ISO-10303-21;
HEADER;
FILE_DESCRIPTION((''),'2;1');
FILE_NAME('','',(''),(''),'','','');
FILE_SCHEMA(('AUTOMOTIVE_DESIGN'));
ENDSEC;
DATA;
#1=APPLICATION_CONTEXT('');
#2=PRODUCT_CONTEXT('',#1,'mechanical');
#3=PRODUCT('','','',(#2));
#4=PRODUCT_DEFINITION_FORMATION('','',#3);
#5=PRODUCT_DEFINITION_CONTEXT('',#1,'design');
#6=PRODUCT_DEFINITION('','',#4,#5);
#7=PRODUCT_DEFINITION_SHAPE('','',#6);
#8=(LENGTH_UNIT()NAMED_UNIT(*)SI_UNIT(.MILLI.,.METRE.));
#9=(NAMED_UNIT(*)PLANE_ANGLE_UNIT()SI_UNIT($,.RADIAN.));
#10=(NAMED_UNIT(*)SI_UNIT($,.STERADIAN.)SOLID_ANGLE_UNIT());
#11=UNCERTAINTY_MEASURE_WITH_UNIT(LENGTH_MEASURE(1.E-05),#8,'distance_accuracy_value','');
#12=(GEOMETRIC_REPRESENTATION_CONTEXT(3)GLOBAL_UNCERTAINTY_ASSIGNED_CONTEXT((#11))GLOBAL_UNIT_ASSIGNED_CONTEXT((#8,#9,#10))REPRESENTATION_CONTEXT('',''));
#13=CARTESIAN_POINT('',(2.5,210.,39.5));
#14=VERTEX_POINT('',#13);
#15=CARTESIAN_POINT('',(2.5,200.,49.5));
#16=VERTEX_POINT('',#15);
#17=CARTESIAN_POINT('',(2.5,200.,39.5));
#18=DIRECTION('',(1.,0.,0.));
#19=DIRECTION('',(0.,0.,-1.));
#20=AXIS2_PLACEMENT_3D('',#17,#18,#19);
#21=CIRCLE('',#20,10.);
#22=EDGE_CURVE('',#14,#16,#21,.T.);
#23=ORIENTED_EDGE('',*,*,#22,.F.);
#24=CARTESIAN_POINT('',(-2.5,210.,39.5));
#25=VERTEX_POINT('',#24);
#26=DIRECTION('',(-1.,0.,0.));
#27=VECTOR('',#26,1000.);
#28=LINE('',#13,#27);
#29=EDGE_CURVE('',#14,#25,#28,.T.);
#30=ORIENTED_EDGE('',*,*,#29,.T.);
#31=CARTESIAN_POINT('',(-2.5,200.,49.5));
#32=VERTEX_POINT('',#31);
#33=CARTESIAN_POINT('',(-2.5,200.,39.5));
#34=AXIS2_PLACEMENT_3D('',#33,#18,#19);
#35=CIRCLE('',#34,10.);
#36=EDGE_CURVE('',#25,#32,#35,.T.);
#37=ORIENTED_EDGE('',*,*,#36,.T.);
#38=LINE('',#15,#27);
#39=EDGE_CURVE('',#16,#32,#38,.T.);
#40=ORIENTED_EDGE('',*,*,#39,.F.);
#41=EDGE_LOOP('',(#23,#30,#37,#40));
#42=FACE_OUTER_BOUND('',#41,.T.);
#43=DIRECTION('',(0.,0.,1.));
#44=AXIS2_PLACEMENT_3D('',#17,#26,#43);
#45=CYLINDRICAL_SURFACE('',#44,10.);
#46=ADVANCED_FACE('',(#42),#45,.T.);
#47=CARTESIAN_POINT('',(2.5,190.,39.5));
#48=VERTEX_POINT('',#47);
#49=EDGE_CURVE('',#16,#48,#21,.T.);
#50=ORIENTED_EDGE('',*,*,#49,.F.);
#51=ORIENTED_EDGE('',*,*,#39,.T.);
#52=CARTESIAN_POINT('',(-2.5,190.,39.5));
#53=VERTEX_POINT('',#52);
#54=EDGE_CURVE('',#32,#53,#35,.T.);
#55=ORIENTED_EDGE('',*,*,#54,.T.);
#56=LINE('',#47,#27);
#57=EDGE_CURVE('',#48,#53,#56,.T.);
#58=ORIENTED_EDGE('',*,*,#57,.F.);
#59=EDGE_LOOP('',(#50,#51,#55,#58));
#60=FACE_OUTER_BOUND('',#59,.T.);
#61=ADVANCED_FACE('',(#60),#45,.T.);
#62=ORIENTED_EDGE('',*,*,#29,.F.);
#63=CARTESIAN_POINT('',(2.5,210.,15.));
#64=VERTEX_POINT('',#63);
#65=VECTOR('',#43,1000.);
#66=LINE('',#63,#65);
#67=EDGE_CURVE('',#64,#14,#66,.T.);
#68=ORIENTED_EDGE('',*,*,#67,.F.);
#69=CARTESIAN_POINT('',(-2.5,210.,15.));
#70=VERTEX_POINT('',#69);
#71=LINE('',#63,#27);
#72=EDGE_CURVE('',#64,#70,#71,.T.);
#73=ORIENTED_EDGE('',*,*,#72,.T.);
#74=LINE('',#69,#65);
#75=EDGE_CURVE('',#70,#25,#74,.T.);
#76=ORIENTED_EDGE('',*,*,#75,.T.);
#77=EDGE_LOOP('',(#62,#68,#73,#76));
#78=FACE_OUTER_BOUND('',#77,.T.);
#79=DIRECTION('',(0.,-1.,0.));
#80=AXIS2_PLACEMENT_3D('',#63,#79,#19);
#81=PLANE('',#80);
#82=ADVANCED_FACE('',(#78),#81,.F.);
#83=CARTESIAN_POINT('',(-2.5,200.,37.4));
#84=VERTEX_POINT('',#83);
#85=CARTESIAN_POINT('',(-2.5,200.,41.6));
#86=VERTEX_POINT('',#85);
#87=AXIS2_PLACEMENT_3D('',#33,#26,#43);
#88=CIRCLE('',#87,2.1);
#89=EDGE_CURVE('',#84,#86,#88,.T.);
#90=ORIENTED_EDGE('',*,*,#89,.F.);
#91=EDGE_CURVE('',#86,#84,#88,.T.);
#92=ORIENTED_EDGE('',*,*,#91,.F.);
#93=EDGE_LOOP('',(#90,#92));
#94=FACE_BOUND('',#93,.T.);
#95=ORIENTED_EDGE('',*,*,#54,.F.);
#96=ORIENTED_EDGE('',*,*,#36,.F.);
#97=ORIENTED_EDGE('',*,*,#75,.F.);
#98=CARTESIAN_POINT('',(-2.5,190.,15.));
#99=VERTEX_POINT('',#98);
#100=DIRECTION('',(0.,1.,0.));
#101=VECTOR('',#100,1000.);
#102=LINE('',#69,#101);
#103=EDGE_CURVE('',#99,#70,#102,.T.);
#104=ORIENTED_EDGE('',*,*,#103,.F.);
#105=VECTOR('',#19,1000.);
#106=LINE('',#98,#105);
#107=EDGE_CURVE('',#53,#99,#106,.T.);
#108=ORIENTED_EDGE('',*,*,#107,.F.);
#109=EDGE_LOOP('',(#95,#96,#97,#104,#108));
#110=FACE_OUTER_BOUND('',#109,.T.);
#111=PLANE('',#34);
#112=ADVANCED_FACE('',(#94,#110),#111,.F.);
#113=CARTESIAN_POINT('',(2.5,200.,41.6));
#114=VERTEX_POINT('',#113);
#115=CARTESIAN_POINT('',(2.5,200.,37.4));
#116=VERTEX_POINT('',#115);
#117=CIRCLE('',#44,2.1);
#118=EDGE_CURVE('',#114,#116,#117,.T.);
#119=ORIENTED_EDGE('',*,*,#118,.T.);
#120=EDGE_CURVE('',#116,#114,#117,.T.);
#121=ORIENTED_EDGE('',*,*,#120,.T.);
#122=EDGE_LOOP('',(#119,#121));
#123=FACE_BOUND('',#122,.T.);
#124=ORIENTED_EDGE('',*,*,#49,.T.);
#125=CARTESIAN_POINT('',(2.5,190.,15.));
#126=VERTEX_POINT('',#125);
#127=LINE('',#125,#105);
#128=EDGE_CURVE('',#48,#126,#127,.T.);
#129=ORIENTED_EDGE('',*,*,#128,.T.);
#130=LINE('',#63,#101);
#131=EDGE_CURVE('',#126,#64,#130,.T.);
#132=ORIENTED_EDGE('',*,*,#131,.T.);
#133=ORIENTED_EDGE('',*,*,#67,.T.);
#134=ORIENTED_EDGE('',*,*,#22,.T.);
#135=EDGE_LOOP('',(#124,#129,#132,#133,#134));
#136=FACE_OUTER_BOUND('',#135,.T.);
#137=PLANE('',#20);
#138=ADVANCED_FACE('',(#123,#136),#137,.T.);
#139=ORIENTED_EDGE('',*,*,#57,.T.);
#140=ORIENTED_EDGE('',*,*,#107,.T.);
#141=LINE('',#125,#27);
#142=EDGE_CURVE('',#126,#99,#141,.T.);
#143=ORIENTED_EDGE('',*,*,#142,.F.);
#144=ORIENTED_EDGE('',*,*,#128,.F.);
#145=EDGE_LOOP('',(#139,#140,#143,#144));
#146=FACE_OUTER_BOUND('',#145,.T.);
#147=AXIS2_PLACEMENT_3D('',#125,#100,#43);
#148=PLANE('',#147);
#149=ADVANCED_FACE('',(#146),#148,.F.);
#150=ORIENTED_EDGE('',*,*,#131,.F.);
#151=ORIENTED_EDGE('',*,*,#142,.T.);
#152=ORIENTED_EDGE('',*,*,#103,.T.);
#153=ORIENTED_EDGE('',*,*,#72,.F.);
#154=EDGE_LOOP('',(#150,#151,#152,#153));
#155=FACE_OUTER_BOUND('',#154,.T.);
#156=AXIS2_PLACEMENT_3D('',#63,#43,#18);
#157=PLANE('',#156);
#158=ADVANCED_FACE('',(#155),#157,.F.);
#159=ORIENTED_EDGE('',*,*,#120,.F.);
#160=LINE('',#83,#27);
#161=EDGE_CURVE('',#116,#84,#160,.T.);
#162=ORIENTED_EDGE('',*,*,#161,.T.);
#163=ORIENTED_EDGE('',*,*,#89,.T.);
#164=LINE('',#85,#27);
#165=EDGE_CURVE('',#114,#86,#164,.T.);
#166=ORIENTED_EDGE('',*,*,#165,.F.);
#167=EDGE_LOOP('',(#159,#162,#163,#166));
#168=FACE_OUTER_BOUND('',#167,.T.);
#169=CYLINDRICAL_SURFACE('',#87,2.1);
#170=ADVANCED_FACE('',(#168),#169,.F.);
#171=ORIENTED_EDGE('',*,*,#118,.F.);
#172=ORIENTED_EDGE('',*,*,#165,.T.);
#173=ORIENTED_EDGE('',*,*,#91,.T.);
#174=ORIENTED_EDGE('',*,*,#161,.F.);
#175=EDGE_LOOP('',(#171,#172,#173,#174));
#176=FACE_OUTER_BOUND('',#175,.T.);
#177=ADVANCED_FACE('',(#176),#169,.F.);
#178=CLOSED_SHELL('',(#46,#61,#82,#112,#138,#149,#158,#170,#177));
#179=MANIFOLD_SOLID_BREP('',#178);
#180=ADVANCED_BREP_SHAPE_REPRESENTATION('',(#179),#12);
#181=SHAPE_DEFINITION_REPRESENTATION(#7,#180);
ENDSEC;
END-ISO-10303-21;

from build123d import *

# Parameters (mm, degrees)
BOSS_EXTRUDE1_DEPTH   = 2.5
M5_TAPPED_HOLE1_D     = 4.2
M5_TAPPED_HOLE1_DEPTH = 5
M5_TAPPED_HOLE1_TIP   = 1.2618073


with BuildPart() as part:
    # Sketch1 → Boss-Extrude1 (new, symmetric)
    with BuildSketch(Plane(origin=(0, 0, 0), x_dir=(0, 0, -1), z_dir=(1, 0, 0))):
        with BuildLine():
            Line((-15, 210), (-39.5, 210))
            ThreePointArc((-39.5, 210), (-49.5, 200), (-39.5, 190))
            Line((-39.5, 190), (-15, 190))
            Line((-15, 190), (-15, 210))
        make_face()
    extrude(amount=BOSS_EXTRUDE1_DEPTH, both=True)

    # M5 Tapped Hole1
    with Locations(Plane(origin=(-2.5, 200, 39.5), x_dir=(0, 0, -1), z_dir=(-1, 0, 0))):
        with Locations((0, 0)):
            Hole(M5_TAPPED_HOLE1_D / 2, depth=M5_TAPPED_HOLE1_DEPTH)
            with Locations((0, 0, -(M5_TAPPED_HOLE1_DEPTH + M5_TAPPED_HOLE1_TIP / 2))):  # 118° drill point
                Cone(0, M5_TAPPED_HOLE1_D / 2, M5_TAPPED_HOLE1_TIP, mode=Mode.SUBTRACT)


solid = part.part
